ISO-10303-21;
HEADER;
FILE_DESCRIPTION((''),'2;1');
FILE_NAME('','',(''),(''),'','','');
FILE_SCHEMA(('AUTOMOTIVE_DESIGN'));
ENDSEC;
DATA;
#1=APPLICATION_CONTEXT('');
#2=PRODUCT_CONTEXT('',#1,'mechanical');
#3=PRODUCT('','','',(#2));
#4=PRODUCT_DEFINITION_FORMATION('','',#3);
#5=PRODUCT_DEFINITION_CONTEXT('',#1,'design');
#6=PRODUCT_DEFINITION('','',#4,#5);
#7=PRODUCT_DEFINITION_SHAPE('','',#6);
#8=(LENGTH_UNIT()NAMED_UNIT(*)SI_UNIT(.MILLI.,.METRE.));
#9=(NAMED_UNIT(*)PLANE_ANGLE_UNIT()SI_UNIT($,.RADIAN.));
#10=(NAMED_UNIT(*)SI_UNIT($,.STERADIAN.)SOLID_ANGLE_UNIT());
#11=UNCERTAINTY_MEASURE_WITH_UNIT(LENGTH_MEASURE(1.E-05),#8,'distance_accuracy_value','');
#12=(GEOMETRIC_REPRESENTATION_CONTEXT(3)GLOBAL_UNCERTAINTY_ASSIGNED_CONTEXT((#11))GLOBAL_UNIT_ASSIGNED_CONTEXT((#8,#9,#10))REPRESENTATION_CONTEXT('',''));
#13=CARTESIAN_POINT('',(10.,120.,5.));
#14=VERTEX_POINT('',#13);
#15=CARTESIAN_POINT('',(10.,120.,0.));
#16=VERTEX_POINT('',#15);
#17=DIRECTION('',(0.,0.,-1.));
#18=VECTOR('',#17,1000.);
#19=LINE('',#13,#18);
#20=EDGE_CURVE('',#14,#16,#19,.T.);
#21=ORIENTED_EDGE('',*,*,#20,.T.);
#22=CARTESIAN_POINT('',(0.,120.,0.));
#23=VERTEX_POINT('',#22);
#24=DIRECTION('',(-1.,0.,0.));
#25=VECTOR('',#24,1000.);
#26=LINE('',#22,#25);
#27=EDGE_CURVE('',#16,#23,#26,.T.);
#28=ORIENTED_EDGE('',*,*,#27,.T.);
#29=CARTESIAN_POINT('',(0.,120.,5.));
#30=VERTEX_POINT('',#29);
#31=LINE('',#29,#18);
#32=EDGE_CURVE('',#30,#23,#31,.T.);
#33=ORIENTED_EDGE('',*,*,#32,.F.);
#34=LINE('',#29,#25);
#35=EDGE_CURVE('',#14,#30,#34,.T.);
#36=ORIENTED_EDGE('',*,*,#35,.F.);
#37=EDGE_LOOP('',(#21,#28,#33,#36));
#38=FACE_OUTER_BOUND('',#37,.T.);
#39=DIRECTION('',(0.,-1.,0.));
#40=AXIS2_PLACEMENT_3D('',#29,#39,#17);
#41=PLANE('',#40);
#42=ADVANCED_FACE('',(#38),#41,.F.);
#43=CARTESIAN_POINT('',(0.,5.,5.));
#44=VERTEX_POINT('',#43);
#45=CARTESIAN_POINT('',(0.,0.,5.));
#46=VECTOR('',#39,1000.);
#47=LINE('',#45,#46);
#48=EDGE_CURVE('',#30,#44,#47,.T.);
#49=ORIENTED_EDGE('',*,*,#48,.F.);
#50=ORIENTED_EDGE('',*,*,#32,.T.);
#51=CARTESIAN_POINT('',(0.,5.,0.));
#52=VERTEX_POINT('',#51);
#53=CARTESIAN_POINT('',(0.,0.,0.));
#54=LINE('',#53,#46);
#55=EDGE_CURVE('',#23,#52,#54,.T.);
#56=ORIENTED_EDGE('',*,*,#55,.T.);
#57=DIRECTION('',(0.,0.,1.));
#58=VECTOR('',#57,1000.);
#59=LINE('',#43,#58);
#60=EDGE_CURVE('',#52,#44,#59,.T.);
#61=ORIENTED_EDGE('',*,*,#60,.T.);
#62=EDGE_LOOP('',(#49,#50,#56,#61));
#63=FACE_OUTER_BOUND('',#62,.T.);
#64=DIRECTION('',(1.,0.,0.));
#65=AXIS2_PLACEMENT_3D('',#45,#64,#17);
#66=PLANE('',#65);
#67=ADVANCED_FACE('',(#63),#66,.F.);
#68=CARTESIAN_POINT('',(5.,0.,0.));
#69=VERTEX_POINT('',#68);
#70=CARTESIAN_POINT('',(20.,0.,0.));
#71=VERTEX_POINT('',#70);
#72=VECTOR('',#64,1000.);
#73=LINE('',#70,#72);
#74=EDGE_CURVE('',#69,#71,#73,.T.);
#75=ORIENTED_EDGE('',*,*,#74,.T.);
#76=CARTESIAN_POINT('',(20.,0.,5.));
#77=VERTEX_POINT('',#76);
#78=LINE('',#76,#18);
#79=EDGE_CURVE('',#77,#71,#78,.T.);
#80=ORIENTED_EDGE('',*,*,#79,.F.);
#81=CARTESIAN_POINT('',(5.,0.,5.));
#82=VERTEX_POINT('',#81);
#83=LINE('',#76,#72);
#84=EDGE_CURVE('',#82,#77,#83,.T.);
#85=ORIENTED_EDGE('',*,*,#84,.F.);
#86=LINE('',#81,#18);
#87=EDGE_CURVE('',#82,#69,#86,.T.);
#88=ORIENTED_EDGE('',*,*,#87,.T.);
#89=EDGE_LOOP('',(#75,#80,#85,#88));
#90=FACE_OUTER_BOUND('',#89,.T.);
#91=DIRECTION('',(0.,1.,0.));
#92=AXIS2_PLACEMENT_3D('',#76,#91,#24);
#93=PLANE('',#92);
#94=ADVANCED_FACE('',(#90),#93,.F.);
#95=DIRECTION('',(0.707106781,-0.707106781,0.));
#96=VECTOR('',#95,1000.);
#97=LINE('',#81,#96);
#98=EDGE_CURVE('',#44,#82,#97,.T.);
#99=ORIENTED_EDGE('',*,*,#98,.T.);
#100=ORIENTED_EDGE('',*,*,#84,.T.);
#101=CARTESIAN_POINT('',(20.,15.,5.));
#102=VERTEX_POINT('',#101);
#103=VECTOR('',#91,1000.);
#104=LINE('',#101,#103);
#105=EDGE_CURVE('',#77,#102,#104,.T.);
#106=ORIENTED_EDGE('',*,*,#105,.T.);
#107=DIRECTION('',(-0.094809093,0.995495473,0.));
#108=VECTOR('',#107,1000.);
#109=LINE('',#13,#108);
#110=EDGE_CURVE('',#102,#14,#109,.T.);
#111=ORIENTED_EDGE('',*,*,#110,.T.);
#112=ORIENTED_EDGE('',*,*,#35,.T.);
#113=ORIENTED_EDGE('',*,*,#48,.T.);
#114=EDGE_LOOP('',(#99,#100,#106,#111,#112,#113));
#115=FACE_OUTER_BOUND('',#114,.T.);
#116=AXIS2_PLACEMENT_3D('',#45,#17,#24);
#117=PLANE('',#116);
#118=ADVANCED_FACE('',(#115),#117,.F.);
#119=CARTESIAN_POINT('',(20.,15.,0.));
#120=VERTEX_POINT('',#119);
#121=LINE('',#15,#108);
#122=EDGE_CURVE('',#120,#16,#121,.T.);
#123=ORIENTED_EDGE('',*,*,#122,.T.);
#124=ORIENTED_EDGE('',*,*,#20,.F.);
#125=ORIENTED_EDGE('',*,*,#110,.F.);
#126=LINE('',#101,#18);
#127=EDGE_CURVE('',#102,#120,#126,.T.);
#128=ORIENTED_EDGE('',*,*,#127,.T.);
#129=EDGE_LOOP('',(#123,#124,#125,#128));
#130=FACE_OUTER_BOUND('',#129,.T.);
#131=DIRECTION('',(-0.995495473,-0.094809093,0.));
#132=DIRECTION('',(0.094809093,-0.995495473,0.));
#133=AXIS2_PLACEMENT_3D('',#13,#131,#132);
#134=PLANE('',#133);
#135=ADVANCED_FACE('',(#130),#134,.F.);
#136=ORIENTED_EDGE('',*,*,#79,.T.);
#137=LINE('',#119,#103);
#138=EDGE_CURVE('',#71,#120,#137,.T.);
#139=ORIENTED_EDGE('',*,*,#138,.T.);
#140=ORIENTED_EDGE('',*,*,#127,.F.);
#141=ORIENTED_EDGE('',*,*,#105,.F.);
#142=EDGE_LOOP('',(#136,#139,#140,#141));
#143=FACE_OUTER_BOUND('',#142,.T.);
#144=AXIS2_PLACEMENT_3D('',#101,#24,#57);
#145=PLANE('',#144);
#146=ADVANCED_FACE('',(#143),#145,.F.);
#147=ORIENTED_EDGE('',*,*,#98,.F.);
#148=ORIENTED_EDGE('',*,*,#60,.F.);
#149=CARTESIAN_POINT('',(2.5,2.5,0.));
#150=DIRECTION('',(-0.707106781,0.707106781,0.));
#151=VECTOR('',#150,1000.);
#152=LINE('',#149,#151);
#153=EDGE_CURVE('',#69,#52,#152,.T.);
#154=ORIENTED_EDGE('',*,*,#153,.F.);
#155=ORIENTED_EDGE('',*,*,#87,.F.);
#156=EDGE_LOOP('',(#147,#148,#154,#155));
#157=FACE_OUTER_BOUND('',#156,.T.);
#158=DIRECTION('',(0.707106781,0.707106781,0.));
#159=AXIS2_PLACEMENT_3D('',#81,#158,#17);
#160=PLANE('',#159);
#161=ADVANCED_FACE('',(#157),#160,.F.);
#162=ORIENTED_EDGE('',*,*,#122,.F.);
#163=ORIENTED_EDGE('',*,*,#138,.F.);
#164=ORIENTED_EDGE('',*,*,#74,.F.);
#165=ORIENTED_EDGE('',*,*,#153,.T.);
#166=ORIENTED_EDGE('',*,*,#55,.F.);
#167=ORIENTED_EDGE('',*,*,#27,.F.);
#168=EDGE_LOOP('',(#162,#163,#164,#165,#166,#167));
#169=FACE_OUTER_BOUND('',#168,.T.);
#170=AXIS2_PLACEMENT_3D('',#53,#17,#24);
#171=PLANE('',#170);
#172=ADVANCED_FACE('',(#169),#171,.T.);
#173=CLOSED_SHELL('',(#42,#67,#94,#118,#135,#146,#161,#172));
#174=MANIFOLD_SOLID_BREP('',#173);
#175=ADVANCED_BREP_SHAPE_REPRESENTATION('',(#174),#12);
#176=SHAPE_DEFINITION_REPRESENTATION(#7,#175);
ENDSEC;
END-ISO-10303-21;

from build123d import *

# Parameters (mm, degrees)
EXTRUDE_1_DEPTH = 5
CHAMFER_1_SIZE  = 5


with BuildPart() as part:
    # 草图1 → 凸台-拉伸1 (new body)
    with BuildSketch(Plane.XY):
        Polygon((0, 0), (0, 120), (10, 120), (20, 15), (20, 0), align=None)
    extrude(amount=EXTRUDE_1_DEPTH)

    # 倒角1
    chamfer_1_edges = [part.edges().sort_by_distance(p)[0] for p in [
        (0, 0, 2.5),
    ]]
    chamfer(chamfer_1_edges, length=CHAMFER_1_SIZE)


solid = part.part
